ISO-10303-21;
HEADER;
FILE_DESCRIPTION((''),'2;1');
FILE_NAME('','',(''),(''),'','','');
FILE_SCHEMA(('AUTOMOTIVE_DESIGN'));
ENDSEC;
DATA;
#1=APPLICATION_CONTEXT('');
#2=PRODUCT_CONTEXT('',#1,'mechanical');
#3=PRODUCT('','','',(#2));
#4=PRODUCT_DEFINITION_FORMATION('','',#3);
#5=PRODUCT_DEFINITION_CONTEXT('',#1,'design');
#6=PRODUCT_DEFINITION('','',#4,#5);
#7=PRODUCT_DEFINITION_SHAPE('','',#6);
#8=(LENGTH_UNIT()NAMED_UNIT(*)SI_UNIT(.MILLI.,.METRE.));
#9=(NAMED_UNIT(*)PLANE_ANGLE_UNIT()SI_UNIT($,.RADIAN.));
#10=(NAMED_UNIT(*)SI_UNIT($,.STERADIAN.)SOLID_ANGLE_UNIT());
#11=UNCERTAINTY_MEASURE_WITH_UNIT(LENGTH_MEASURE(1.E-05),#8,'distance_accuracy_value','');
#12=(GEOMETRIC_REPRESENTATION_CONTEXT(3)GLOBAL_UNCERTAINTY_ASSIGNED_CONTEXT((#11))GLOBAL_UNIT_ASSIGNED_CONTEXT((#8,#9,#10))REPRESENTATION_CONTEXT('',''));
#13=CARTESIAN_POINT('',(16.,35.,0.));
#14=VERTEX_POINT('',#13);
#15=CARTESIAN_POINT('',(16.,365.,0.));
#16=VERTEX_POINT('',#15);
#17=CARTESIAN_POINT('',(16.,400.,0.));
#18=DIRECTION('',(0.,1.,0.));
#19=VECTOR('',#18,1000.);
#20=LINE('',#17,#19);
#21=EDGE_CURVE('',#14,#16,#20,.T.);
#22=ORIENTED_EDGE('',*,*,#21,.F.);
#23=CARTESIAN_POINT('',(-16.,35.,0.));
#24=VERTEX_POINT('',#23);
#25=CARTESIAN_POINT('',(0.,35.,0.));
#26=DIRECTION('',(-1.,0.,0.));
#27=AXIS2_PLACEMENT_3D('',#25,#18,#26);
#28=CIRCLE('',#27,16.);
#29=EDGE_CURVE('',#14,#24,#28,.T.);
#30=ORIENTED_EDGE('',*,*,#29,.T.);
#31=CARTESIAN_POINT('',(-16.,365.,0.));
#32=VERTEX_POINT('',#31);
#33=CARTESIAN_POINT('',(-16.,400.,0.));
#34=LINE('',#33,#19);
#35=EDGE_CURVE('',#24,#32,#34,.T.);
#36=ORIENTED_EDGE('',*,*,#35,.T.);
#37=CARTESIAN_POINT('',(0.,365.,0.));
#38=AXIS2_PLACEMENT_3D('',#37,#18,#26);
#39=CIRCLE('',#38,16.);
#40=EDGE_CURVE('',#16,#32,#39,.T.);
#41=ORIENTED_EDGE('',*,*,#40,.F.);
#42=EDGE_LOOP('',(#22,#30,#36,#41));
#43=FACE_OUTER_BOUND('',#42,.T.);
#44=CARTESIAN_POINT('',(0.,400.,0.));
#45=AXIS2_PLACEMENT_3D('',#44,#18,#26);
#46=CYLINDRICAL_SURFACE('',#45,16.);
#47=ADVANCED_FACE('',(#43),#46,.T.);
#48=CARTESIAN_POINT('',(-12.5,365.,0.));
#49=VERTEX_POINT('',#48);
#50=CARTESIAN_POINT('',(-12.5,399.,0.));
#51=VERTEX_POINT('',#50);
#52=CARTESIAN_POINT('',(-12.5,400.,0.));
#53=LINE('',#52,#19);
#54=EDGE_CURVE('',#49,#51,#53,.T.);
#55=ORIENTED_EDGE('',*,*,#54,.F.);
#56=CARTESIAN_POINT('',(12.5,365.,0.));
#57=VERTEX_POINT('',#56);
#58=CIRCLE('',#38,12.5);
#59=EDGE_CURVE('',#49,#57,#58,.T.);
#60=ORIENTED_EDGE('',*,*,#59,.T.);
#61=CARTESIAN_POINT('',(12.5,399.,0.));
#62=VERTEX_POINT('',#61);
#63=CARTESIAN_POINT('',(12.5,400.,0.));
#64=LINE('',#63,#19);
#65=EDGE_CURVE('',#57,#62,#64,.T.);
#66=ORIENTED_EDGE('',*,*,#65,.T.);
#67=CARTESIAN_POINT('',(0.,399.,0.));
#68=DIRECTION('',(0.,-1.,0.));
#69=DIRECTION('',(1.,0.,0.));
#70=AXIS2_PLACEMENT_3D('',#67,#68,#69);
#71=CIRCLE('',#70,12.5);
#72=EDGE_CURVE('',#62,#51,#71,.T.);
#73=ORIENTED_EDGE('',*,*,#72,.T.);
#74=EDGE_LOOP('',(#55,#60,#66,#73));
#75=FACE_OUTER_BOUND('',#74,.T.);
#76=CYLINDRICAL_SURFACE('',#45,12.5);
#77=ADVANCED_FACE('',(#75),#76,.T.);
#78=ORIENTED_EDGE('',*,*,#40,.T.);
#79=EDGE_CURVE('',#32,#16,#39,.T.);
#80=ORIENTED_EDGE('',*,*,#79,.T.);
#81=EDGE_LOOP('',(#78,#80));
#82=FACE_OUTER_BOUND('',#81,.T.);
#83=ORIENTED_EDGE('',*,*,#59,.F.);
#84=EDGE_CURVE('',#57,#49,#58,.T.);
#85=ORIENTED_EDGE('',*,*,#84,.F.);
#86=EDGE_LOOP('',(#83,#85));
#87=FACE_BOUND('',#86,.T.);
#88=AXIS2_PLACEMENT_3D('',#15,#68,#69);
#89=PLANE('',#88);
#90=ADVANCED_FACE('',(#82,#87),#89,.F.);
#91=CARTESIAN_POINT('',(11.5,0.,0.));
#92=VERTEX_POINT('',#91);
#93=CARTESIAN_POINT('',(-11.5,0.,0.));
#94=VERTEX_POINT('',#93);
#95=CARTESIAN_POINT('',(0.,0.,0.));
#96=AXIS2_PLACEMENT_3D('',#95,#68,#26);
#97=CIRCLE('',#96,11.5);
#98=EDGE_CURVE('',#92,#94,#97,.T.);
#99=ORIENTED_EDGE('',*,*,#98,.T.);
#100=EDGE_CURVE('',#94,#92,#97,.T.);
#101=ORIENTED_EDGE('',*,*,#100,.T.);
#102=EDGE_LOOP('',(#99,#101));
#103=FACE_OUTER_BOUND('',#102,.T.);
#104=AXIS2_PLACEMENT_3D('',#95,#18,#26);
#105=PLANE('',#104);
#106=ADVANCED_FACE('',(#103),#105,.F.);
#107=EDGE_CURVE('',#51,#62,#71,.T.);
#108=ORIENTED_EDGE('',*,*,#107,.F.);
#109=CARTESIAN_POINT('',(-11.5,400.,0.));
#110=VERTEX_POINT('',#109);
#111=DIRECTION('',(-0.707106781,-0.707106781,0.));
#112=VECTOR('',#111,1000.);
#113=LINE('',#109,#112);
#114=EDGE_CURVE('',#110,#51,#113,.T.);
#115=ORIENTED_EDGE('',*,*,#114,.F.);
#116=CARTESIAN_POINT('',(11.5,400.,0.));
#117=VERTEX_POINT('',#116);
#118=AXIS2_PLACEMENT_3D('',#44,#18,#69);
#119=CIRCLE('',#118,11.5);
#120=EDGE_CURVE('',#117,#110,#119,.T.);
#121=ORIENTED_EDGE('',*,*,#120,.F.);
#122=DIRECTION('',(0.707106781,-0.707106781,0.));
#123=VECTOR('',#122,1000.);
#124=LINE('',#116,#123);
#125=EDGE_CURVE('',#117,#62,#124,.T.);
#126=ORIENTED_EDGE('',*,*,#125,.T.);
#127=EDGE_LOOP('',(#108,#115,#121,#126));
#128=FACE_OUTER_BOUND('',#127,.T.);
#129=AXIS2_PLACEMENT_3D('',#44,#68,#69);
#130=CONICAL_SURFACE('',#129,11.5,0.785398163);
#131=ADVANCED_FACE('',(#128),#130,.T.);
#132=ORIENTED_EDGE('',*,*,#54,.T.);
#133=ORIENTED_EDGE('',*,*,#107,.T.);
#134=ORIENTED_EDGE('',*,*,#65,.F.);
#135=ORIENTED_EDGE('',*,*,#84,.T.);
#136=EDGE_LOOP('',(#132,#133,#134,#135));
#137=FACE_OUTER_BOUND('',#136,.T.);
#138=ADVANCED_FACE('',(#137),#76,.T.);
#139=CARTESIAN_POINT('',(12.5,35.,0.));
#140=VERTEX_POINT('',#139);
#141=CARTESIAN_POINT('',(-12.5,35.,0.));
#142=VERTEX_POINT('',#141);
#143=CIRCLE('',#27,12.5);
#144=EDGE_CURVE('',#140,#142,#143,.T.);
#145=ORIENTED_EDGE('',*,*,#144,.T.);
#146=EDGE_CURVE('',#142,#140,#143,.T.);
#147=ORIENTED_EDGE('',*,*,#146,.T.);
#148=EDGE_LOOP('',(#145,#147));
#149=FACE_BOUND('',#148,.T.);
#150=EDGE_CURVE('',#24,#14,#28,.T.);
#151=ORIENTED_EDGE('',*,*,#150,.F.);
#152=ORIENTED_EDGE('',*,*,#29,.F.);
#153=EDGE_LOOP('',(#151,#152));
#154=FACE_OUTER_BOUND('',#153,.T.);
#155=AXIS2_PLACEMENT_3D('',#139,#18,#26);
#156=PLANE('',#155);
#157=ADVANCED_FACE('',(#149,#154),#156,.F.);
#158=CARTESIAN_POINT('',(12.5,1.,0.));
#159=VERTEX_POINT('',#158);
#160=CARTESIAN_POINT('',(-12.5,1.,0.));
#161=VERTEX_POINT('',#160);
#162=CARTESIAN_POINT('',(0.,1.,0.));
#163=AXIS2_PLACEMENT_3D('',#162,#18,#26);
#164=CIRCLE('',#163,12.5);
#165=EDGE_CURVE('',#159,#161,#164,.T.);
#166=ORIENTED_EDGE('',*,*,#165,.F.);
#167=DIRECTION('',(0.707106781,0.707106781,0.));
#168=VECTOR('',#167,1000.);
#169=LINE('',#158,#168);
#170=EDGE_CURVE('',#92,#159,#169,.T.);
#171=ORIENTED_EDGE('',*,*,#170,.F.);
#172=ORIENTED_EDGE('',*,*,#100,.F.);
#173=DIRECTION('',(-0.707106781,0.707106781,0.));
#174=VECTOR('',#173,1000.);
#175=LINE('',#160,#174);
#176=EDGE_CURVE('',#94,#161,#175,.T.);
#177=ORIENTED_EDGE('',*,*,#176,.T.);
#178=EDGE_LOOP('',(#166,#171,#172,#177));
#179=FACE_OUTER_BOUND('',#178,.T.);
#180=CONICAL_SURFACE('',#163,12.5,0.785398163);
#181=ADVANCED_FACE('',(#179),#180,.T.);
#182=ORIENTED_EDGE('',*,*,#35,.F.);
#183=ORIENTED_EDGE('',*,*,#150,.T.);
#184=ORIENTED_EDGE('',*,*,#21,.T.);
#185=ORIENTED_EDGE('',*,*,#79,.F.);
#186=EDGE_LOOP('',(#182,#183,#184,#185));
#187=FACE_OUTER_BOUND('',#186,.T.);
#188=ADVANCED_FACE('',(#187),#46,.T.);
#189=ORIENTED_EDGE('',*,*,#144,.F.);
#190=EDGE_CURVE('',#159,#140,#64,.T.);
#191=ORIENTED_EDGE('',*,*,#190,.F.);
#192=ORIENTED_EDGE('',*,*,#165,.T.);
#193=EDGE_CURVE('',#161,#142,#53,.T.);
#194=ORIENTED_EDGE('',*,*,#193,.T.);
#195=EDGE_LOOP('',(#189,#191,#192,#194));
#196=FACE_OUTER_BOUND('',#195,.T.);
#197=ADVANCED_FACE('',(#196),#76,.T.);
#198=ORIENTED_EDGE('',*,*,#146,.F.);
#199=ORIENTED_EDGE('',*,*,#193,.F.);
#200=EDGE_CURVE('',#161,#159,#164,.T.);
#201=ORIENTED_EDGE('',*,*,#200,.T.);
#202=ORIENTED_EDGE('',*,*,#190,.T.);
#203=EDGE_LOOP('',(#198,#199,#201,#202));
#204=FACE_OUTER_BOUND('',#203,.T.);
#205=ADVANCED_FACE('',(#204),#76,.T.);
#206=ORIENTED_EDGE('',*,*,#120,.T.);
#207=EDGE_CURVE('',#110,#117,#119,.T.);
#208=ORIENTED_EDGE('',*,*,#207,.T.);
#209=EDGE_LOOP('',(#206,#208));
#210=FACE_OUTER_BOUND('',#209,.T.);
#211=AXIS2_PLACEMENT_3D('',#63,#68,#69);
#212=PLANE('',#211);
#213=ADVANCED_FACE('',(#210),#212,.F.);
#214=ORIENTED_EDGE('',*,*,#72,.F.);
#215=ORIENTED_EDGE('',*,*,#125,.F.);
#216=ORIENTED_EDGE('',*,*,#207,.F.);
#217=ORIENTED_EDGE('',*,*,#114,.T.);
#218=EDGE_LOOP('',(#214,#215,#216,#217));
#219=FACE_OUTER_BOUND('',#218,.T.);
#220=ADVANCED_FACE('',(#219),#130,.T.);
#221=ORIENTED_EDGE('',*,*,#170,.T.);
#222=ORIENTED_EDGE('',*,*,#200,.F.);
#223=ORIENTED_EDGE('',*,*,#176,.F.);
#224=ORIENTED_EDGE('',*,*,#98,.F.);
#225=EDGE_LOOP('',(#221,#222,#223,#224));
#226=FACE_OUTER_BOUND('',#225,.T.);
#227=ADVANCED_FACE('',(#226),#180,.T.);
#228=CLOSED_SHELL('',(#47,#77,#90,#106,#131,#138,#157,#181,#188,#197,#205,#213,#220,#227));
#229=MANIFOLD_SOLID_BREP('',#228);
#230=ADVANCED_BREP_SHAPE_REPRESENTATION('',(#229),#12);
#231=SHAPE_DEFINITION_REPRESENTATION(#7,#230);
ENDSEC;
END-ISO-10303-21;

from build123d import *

# Parameters (mm, degrees)
CHAMFER1_SIZE = 1


with BuildPart() as part:
    # Sketch1 → Revolve1 (revolve)
    with BuildSketch(Plane.XY, mode=Mode.PRIVATE) as revolve1_sk:
        Polygon((0, 0), (12.5, 0), (12.5, 35), (16, 35), (16, 365), (12.5, 365), (12.5, 400), (0, 400), align=None)
    revolve(revolve1_sk.sketch.rotate(Axis((0, 400, 0), (0, -1, 0)), 180), axis=Axis((0, 400, 0), (0, -1, 0)))

    # Chamfer1
    chamfer1_edges = [part.edges().sort_by_distance(p)[0] for p in [
        (12.5, 400, 0),
        (12.5, 0, 0),
    ]]
    chamfer(chamfer1_edges, length=CHAMFER1_SIZE)


solid = part.part
